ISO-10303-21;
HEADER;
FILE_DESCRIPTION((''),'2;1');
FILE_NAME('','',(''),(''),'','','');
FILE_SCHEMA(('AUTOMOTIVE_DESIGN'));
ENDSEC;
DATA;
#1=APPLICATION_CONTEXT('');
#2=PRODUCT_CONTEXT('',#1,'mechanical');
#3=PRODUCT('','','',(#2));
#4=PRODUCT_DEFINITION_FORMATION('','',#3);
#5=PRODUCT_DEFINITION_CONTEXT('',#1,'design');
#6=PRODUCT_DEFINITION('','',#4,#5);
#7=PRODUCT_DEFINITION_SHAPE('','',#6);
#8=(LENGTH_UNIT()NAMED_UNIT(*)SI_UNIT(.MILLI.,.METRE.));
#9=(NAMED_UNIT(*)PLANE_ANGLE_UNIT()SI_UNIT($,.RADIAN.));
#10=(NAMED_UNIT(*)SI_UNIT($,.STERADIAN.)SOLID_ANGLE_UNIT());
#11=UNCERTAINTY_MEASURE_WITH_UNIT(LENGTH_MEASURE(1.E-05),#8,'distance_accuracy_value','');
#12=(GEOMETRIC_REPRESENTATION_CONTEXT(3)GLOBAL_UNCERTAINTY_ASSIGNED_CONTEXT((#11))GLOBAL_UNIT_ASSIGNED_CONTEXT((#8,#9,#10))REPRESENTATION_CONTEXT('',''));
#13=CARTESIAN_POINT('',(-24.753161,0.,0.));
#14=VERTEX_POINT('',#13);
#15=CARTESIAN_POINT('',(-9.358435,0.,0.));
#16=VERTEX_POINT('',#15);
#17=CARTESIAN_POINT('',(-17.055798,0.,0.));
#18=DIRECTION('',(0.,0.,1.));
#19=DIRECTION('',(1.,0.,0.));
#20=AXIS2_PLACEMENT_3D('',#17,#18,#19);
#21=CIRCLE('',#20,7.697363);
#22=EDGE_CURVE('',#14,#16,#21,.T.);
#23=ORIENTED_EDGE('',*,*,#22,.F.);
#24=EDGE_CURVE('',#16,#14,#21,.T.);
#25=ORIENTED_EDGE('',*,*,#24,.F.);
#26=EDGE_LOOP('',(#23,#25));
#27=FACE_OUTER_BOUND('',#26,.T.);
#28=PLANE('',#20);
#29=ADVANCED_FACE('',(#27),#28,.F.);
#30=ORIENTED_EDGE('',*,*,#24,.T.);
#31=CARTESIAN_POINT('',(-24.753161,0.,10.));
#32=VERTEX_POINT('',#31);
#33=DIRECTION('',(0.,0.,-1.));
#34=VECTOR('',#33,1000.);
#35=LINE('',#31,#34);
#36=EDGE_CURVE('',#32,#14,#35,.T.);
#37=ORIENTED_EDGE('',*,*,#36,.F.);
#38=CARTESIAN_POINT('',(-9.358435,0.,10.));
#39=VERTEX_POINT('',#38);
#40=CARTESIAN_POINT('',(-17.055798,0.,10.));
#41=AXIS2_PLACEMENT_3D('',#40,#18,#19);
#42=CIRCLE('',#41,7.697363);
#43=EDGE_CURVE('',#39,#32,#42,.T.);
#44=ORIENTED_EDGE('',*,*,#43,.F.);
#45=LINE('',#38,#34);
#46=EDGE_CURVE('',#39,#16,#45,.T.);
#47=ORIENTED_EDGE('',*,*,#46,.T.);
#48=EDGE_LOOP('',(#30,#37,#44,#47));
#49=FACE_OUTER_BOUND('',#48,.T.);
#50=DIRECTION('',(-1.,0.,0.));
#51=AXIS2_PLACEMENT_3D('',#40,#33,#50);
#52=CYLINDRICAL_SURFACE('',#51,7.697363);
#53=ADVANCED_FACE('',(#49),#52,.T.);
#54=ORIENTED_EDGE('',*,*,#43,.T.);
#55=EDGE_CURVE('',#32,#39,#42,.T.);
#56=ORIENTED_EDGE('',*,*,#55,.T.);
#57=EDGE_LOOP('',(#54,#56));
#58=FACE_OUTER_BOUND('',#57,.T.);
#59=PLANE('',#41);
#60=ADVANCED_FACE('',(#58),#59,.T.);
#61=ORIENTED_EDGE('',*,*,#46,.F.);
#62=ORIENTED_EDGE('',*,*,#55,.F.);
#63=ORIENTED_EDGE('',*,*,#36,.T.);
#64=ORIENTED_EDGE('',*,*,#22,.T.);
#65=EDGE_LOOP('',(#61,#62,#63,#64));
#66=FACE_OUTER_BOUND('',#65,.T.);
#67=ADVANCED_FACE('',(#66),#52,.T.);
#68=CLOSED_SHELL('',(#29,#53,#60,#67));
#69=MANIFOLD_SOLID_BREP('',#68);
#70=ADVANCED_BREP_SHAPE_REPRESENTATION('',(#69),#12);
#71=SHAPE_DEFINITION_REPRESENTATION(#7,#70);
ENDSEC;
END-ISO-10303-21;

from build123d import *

# Parameters (mm, degrees)
SKETCH1_R           = 7.6973628
BOSS_EXTRUDE1_DEPTH = 10


with BuildPart() as part:
    # Sketch1 → Boss-Extrude1 (new body)
    with BuildSketch(Plane.XY):
        with Locations((-17.055797946, 0)):
            Circle(SKETCH1_R)
    extrude(amount=BOSS_EXTRUDE1_DEPTH)


solid = part.part
